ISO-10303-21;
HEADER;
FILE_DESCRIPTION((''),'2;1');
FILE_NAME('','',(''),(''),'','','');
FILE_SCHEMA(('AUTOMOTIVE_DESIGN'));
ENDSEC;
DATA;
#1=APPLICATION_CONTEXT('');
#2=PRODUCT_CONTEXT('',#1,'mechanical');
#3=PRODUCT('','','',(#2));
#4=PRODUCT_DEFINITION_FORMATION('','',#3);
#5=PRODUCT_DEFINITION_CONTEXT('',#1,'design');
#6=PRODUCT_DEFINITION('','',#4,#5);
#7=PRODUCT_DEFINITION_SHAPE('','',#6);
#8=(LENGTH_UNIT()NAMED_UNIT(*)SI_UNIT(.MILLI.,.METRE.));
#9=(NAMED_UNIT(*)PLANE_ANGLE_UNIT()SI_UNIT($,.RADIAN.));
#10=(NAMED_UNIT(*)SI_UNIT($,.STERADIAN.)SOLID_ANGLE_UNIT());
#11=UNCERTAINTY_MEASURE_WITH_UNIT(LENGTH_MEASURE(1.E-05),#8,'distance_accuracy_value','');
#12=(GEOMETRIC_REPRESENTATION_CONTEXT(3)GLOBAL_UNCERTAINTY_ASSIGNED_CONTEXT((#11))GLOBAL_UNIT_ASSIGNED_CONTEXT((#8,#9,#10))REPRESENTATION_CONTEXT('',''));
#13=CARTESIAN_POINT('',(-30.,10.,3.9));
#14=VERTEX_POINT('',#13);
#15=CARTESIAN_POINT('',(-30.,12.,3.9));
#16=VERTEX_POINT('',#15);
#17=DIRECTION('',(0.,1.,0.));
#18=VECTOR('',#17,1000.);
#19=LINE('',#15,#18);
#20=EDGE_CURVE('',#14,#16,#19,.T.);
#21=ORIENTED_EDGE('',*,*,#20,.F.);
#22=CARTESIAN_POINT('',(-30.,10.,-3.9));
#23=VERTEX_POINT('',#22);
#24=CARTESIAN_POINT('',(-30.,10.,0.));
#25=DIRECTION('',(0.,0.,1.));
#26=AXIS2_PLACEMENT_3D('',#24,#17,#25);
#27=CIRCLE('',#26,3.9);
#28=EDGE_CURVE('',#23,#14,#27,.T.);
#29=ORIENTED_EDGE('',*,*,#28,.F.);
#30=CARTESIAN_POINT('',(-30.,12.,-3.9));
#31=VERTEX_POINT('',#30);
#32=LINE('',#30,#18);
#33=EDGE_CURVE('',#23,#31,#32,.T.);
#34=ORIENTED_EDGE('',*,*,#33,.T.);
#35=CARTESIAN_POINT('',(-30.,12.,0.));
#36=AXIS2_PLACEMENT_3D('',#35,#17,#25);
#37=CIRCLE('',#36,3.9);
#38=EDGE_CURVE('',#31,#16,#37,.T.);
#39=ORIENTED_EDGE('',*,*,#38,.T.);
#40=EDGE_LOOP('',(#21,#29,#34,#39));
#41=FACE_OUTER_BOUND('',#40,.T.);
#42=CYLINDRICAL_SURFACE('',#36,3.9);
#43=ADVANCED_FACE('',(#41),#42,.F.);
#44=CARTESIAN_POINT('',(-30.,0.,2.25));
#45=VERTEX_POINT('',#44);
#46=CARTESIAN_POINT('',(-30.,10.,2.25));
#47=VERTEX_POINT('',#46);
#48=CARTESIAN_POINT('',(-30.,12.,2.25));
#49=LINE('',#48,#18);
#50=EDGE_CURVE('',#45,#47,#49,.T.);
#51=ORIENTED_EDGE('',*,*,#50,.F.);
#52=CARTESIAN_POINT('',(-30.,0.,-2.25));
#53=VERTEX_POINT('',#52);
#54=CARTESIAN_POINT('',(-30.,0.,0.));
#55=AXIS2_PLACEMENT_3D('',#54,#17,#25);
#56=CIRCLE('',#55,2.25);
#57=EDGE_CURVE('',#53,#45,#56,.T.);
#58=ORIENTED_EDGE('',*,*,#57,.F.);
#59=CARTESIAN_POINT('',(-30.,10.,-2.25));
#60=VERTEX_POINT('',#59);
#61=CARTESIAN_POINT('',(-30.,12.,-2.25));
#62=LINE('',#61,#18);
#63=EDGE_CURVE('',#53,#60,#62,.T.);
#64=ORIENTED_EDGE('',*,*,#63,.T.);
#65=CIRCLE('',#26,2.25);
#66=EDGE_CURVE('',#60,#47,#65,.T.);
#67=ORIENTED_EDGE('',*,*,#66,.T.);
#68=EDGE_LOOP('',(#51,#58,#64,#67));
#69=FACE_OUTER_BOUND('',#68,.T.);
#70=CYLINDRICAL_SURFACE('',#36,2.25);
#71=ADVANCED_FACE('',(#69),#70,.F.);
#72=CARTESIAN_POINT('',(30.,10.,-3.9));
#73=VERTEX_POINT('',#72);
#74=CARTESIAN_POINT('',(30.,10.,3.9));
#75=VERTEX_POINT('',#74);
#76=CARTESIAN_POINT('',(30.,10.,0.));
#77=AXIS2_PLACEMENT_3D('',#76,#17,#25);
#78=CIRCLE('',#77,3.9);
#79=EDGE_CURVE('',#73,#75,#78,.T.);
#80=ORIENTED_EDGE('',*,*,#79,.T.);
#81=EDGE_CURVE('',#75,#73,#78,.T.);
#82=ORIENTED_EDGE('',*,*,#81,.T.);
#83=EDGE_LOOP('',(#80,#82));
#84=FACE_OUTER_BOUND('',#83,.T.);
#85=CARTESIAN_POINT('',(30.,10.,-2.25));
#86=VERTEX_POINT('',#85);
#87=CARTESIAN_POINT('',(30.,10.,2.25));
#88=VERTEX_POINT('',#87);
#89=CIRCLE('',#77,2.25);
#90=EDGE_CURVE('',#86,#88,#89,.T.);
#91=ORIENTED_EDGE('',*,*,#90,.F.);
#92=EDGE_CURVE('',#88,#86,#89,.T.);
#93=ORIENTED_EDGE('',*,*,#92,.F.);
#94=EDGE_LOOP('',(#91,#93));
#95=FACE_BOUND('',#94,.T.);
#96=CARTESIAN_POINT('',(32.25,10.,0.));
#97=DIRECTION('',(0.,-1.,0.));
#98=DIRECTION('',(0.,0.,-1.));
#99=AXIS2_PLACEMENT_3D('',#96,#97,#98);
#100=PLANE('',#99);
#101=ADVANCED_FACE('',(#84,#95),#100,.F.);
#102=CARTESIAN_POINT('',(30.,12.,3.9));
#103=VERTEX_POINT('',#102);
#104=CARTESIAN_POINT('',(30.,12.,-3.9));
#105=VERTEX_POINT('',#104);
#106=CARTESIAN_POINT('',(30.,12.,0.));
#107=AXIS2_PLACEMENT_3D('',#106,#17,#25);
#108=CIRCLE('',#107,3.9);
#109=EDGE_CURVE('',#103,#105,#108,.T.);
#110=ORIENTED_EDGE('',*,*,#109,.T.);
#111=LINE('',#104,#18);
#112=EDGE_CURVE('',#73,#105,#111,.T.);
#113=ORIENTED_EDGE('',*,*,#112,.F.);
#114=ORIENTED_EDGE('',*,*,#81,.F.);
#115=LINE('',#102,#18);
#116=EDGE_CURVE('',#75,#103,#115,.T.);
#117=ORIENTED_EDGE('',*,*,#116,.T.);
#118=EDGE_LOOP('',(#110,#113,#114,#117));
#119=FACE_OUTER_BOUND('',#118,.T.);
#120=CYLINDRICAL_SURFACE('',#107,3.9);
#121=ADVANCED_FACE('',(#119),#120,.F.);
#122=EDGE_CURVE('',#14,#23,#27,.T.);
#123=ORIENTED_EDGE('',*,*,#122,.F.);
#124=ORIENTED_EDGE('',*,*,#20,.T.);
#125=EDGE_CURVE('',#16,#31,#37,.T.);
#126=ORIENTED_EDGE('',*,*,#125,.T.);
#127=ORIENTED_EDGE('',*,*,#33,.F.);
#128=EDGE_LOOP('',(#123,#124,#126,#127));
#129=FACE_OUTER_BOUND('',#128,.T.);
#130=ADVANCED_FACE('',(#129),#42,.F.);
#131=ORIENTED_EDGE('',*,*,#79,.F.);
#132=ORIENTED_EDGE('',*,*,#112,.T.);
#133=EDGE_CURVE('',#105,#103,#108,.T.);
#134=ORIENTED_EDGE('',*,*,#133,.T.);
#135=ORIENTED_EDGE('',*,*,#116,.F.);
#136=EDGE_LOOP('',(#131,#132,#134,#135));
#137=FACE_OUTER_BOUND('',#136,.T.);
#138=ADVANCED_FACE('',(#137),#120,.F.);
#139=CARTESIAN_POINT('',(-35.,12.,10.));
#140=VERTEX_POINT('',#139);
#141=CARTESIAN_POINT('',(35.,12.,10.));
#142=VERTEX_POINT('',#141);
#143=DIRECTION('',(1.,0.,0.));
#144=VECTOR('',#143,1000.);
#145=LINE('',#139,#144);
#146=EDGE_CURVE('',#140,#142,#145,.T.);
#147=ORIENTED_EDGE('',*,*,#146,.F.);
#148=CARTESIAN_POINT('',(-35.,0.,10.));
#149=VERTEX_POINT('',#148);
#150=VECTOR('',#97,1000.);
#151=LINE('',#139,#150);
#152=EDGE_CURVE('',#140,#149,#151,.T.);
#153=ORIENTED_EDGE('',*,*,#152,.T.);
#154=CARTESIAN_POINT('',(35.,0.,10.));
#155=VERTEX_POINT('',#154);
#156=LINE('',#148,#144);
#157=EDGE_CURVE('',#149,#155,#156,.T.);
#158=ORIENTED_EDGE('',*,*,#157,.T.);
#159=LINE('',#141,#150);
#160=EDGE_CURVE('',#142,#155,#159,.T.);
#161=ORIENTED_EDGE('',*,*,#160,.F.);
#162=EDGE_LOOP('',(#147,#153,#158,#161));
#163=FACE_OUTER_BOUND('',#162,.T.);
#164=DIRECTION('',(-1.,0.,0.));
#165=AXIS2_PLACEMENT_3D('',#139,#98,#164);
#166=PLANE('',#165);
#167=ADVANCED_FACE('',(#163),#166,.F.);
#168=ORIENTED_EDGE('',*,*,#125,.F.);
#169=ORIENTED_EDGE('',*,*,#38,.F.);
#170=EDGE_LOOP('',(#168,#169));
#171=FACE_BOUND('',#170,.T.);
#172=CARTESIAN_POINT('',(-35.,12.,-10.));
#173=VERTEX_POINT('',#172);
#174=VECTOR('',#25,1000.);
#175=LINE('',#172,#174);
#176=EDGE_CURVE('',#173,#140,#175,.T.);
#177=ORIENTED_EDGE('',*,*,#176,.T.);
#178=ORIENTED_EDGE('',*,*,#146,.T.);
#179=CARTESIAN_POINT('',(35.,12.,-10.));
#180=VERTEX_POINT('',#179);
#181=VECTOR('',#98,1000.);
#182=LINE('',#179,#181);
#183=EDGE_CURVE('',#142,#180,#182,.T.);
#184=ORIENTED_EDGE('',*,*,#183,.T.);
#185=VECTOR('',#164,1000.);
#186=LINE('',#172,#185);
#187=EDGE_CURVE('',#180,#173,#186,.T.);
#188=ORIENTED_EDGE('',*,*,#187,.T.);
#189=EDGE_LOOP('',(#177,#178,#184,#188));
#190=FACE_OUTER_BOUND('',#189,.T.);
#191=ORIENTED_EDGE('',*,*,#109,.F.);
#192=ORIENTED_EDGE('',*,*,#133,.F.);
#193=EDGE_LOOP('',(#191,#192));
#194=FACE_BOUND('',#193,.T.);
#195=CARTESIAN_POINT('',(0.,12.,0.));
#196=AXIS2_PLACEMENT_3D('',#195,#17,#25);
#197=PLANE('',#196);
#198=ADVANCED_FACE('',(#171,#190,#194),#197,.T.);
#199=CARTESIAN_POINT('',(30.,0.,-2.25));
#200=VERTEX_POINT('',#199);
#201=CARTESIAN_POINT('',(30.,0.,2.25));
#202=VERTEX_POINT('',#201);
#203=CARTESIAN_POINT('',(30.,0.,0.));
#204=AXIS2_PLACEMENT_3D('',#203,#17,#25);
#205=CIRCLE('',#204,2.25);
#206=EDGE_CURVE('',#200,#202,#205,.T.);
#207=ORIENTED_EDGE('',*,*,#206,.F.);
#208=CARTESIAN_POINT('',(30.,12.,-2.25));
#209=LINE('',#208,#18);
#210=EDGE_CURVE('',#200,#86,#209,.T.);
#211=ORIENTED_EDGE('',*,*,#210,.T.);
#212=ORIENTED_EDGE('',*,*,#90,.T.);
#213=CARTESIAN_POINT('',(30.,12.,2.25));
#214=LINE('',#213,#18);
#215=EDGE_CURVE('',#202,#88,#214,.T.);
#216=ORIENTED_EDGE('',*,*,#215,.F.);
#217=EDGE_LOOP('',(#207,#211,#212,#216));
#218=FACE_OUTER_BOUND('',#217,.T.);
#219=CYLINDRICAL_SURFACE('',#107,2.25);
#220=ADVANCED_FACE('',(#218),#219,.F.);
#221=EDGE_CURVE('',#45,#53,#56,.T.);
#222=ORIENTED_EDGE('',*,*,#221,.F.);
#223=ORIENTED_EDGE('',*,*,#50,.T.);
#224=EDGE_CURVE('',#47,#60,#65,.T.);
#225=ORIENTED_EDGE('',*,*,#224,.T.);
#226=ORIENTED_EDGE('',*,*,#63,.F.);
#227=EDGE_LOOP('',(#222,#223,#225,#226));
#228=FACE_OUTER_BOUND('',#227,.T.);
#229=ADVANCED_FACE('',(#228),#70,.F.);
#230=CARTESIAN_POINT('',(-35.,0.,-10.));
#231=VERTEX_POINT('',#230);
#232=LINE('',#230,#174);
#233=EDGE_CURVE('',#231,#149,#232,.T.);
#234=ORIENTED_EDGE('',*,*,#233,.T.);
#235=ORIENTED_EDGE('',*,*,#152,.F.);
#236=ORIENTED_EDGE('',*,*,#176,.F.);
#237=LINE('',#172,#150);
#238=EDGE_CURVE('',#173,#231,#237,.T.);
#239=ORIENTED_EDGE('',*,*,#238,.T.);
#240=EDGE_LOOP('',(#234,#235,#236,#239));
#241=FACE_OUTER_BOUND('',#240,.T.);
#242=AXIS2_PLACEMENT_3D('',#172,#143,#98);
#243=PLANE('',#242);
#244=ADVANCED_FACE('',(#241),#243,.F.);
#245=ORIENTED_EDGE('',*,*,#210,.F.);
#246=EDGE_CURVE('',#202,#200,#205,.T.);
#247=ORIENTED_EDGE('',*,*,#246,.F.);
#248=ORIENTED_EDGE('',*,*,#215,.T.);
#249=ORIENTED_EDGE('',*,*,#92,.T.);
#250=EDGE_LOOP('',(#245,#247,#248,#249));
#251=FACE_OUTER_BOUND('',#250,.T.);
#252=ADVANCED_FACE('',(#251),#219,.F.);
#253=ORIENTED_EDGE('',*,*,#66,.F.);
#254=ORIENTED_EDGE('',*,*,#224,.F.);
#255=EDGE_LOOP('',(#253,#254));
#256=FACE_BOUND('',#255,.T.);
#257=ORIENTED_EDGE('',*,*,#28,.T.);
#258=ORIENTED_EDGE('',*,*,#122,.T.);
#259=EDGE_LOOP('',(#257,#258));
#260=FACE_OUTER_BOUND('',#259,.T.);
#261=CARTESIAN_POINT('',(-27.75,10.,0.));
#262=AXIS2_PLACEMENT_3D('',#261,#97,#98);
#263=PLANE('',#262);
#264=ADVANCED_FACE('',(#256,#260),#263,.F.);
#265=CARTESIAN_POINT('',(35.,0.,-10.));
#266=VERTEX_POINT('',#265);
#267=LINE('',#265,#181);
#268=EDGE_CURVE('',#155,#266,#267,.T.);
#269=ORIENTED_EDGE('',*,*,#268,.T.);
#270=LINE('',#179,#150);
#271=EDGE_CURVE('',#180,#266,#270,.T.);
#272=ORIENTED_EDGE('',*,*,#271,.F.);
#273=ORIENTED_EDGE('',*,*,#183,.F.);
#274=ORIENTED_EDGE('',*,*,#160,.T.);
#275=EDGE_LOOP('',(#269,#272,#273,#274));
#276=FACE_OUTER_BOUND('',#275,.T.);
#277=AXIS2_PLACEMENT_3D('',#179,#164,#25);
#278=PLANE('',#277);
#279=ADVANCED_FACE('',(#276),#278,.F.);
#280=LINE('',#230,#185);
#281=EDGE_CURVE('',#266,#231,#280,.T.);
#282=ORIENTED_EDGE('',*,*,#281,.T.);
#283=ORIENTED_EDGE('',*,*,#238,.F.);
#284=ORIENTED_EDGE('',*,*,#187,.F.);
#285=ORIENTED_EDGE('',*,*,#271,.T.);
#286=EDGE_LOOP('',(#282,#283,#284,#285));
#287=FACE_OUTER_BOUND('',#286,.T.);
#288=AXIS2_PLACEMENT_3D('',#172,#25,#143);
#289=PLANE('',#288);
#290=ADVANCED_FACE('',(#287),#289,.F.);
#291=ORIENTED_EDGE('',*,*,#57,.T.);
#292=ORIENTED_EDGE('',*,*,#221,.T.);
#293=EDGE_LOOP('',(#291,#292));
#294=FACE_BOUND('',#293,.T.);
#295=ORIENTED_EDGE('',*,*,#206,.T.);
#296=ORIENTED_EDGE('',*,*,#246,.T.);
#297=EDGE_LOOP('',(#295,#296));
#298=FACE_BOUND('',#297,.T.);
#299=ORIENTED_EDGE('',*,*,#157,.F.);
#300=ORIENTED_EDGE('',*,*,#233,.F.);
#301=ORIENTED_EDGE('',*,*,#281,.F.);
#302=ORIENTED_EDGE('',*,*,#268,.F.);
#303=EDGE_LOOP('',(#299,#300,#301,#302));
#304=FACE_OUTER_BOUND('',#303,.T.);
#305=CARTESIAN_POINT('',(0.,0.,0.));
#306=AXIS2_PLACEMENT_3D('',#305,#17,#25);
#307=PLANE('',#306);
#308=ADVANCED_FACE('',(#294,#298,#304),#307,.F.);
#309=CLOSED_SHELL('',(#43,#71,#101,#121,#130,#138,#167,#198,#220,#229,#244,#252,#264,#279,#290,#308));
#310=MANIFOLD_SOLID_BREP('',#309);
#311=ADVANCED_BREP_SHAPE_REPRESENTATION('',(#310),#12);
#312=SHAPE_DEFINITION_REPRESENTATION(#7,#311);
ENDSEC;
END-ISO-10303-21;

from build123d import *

# Parameters (mm, degrees)
SKETCH_1_W                = 70
SKETCH_1_H                = 20
EXTRUDE_1_DEPTH           = 12
HOLE_WIZARD_1_D           = 4.5
HOLE_WIZARD_1_CBORE_D     = 7.8
HOLE_WIZARD_1_CBORE_DEPTH = 2


with BuildPart() as part:
    # 草图1 → 凸台-拉伸1 (new body)
    with BuildSketch(Plane(origin=(0, 0, 0), x_dir=(1, 0, 0), z_dir=(0, 1, 0))):
        Rectangle(SKETCH_1_W, SKETCH_1_H)
    extrude(amount=EXTRUDE_1_DEPTH)

    # 打孔尺寸(%根据)内六角圆柱头螺钉的类型1 (through all)
    with Locations(Plane(origin=(0, 12, 0), x_dir=(1, 0, 0), z_dir=(0, 1, 0))):
        with Locations((-30, 0), (30, 0)):
            CounterBoreHole(HOLE_WIZARD_1_D / 2, HOLE_WIZARD_1_CBORE_D / 2, HOLE_WIZARD_1_CBORE_DEPTH)


solid = part.part
